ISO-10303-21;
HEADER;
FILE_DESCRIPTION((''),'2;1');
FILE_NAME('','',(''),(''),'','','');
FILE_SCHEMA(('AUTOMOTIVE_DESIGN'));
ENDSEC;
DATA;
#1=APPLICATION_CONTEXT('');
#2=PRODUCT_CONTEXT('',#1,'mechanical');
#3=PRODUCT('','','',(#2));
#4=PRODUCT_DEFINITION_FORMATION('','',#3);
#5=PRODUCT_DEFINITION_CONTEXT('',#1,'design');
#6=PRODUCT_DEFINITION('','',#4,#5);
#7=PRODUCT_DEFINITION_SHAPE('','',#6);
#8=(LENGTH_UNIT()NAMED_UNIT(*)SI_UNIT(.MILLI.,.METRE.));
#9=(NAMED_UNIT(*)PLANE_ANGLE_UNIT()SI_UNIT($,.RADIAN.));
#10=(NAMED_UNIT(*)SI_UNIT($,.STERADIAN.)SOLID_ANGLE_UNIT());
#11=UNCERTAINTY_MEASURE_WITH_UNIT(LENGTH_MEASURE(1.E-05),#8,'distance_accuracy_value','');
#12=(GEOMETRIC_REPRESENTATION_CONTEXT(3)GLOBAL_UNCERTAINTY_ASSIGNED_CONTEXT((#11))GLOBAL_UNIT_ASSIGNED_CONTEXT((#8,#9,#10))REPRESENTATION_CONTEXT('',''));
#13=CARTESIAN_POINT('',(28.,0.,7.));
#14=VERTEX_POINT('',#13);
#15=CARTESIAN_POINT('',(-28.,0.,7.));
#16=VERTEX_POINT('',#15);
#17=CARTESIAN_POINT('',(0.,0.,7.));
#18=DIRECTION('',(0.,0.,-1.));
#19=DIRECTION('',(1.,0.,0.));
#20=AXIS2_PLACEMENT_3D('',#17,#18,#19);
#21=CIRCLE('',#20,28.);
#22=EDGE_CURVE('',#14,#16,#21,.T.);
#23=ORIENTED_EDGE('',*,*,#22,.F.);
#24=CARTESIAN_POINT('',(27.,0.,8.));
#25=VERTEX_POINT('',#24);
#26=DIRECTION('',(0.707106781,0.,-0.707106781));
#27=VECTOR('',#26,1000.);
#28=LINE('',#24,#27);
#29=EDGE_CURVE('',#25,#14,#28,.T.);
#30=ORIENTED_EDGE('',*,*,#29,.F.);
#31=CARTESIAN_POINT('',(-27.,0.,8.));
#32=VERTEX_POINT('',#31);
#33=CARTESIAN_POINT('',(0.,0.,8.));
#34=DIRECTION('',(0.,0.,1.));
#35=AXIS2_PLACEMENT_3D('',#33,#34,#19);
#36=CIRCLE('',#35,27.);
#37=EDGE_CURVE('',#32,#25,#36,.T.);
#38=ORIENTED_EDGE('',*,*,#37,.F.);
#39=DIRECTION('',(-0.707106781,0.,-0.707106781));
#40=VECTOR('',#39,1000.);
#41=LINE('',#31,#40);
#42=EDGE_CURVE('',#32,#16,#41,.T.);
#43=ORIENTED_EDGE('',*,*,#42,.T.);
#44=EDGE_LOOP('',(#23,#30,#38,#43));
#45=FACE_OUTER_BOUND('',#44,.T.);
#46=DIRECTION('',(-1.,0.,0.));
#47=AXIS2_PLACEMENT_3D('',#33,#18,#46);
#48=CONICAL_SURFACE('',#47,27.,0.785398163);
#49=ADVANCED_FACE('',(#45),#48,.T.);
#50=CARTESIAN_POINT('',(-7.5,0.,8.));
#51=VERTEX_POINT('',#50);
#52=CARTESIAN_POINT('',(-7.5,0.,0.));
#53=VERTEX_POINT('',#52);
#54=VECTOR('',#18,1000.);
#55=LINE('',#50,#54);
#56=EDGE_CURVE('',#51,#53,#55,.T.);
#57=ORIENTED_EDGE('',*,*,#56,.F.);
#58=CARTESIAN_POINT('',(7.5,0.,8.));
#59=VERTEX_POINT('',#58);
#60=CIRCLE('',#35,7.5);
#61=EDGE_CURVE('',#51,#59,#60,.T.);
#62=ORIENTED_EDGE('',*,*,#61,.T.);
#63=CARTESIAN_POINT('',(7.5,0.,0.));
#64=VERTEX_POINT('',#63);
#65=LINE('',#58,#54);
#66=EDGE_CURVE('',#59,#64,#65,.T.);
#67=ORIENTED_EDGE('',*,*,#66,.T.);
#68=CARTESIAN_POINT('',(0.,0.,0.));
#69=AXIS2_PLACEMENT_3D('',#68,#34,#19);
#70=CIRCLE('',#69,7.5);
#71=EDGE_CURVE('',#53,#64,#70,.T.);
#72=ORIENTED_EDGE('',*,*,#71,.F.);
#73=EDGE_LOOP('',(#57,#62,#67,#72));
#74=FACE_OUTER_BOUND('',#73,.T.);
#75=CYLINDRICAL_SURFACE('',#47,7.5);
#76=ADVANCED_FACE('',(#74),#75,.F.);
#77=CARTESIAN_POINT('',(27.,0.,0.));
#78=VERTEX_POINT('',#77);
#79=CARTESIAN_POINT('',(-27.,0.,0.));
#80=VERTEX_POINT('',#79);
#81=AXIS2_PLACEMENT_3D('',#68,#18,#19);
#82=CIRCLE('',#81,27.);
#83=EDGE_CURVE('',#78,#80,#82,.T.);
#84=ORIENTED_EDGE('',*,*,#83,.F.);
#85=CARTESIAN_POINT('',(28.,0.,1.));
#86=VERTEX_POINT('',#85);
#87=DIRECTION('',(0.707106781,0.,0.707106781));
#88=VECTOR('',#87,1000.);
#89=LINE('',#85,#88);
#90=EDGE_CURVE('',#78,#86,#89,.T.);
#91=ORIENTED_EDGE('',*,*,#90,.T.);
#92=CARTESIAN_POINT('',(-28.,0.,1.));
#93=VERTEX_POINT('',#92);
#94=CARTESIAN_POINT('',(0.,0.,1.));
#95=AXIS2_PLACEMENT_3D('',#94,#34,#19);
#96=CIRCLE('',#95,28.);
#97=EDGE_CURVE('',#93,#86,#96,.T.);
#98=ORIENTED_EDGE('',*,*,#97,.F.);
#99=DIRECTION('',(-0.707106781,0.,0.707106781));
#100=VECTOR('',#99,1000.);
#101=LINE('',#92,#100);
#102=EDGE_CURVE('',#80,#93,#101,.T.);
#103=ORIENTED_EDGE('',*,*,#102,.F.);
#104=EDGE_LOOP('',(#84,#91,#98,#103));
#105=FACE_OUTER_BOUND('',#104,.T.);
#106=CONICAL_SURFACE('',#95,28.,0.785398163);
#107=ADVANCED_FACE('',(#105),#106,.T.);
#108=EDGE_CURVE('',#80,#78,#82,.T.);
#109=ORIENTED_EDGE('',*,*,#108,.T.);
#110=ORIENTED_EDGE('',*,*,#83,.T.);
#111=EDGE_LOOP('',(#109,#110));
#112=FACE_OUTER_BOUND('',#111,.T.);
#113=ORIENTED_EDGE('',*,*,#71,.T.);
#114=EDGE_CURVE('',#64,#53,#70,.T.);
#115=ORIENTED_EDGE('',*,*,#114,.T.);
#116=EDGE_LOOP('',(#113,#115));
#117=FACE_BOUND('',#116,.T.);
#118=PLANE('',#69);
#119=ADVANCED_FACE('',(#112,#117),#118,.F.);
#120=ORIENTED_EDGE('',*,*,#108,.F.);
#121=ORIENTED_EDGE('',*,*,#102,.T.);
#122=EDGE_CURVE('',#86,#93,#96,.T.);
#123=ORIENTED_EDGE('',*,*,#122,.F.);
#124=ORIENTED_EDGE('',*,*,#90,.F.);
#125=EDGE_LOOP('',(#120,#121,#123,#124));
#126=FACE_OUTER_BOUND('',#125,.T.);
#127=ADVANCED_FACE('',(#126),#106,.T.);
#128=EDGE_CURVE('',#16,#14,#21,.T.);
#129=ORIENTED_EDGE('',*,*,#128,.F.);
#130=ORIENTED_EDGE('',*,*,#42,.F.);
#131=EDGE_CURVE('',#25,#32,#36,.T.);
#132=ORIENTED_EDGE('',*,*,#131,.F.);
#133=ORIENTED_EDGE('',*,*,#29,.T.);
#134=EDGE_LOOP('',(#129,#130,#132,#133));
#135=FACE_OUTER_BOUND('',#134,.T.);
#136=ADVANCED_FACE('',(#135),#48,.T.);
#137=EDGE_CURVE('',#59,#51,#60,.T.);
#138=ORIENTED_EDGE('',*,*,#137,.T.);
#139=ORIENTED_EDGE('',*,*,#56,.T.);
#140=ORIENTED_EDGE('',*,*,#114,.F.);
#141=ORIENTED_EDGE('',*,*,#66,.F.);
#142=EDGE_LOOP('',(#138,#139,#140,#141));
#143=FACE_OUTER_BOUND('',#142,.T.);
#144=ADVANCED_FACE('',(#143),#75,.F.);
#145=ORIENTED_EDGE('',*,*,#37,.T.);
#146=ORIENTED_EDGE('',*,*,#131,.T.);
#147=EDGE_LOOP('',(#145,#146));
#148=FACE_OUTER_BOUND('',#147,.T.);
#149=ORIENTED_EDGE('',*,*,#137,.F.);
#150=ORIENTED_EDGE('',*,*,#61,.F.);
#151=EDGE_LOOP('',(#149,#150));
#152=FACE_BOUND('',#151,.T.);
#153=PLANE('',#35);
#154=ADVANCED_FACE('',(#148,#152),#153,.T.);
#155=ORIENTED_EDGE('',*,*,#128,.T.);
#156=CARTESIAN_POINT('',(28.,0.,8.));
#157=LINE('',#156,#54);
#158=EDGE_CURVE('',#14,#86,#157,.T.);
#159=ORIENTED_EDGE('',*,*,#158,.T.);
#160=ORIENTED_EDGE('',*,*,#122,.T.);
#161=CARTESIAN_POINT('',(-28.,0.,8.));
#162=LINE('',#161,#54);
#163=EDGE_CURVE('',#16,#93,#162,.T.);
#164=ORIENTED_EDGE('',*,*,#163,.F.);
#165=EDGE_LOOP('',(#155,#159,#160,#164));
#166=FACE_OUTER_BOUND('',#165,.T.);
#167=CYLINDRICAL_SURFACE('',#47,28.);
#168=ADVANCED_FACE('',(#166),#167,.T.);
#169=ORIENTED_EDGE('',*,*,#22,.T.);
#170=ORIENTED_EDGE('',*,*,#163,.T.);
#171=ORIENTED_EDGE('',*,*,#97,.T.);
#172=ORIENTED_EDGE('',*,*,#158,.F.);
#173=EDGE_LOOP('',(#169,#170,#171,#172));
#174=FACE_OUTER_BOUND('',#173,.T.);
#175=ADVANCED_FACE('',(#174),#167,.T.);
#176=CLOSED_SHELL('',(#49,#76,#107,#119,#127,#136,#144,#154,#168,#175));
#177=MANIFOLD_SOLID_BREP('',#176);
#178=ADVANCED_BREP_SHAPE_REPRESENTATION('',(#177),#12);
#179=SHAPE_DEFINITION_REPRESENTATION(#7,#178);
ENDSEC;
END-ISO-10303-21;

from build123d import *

# Parameters (mm, degrees)
SKETCH_1_R      = 28
SKETCH_1_R_2    = 7.5
EXTRUDE_1_DEPTH = 8
CHAMFER_1_SIZE  = 1


with BuildPart() as part:
    # 草图1 → 凸台-拉伸1 (new body)
    with BuildSketch(Plane.XY):
        Circle(SKETCH_1_R)
        Circle(SKETCH_1_R_2, mode=Mode.SUBTRACT)
    extrude(amount=EXTRUDE_1_DEPTH)

    # 倒角1
    chamfer_1_edges = [part.edges().sort_by_distance(p)[0] for p in [
        (-28, 0, 0),
        (-28, 0, 8),
    ]]
    chamfer(chamfer_1_edges, length=CHAMFER_1_SIZE)


solid = part.part
